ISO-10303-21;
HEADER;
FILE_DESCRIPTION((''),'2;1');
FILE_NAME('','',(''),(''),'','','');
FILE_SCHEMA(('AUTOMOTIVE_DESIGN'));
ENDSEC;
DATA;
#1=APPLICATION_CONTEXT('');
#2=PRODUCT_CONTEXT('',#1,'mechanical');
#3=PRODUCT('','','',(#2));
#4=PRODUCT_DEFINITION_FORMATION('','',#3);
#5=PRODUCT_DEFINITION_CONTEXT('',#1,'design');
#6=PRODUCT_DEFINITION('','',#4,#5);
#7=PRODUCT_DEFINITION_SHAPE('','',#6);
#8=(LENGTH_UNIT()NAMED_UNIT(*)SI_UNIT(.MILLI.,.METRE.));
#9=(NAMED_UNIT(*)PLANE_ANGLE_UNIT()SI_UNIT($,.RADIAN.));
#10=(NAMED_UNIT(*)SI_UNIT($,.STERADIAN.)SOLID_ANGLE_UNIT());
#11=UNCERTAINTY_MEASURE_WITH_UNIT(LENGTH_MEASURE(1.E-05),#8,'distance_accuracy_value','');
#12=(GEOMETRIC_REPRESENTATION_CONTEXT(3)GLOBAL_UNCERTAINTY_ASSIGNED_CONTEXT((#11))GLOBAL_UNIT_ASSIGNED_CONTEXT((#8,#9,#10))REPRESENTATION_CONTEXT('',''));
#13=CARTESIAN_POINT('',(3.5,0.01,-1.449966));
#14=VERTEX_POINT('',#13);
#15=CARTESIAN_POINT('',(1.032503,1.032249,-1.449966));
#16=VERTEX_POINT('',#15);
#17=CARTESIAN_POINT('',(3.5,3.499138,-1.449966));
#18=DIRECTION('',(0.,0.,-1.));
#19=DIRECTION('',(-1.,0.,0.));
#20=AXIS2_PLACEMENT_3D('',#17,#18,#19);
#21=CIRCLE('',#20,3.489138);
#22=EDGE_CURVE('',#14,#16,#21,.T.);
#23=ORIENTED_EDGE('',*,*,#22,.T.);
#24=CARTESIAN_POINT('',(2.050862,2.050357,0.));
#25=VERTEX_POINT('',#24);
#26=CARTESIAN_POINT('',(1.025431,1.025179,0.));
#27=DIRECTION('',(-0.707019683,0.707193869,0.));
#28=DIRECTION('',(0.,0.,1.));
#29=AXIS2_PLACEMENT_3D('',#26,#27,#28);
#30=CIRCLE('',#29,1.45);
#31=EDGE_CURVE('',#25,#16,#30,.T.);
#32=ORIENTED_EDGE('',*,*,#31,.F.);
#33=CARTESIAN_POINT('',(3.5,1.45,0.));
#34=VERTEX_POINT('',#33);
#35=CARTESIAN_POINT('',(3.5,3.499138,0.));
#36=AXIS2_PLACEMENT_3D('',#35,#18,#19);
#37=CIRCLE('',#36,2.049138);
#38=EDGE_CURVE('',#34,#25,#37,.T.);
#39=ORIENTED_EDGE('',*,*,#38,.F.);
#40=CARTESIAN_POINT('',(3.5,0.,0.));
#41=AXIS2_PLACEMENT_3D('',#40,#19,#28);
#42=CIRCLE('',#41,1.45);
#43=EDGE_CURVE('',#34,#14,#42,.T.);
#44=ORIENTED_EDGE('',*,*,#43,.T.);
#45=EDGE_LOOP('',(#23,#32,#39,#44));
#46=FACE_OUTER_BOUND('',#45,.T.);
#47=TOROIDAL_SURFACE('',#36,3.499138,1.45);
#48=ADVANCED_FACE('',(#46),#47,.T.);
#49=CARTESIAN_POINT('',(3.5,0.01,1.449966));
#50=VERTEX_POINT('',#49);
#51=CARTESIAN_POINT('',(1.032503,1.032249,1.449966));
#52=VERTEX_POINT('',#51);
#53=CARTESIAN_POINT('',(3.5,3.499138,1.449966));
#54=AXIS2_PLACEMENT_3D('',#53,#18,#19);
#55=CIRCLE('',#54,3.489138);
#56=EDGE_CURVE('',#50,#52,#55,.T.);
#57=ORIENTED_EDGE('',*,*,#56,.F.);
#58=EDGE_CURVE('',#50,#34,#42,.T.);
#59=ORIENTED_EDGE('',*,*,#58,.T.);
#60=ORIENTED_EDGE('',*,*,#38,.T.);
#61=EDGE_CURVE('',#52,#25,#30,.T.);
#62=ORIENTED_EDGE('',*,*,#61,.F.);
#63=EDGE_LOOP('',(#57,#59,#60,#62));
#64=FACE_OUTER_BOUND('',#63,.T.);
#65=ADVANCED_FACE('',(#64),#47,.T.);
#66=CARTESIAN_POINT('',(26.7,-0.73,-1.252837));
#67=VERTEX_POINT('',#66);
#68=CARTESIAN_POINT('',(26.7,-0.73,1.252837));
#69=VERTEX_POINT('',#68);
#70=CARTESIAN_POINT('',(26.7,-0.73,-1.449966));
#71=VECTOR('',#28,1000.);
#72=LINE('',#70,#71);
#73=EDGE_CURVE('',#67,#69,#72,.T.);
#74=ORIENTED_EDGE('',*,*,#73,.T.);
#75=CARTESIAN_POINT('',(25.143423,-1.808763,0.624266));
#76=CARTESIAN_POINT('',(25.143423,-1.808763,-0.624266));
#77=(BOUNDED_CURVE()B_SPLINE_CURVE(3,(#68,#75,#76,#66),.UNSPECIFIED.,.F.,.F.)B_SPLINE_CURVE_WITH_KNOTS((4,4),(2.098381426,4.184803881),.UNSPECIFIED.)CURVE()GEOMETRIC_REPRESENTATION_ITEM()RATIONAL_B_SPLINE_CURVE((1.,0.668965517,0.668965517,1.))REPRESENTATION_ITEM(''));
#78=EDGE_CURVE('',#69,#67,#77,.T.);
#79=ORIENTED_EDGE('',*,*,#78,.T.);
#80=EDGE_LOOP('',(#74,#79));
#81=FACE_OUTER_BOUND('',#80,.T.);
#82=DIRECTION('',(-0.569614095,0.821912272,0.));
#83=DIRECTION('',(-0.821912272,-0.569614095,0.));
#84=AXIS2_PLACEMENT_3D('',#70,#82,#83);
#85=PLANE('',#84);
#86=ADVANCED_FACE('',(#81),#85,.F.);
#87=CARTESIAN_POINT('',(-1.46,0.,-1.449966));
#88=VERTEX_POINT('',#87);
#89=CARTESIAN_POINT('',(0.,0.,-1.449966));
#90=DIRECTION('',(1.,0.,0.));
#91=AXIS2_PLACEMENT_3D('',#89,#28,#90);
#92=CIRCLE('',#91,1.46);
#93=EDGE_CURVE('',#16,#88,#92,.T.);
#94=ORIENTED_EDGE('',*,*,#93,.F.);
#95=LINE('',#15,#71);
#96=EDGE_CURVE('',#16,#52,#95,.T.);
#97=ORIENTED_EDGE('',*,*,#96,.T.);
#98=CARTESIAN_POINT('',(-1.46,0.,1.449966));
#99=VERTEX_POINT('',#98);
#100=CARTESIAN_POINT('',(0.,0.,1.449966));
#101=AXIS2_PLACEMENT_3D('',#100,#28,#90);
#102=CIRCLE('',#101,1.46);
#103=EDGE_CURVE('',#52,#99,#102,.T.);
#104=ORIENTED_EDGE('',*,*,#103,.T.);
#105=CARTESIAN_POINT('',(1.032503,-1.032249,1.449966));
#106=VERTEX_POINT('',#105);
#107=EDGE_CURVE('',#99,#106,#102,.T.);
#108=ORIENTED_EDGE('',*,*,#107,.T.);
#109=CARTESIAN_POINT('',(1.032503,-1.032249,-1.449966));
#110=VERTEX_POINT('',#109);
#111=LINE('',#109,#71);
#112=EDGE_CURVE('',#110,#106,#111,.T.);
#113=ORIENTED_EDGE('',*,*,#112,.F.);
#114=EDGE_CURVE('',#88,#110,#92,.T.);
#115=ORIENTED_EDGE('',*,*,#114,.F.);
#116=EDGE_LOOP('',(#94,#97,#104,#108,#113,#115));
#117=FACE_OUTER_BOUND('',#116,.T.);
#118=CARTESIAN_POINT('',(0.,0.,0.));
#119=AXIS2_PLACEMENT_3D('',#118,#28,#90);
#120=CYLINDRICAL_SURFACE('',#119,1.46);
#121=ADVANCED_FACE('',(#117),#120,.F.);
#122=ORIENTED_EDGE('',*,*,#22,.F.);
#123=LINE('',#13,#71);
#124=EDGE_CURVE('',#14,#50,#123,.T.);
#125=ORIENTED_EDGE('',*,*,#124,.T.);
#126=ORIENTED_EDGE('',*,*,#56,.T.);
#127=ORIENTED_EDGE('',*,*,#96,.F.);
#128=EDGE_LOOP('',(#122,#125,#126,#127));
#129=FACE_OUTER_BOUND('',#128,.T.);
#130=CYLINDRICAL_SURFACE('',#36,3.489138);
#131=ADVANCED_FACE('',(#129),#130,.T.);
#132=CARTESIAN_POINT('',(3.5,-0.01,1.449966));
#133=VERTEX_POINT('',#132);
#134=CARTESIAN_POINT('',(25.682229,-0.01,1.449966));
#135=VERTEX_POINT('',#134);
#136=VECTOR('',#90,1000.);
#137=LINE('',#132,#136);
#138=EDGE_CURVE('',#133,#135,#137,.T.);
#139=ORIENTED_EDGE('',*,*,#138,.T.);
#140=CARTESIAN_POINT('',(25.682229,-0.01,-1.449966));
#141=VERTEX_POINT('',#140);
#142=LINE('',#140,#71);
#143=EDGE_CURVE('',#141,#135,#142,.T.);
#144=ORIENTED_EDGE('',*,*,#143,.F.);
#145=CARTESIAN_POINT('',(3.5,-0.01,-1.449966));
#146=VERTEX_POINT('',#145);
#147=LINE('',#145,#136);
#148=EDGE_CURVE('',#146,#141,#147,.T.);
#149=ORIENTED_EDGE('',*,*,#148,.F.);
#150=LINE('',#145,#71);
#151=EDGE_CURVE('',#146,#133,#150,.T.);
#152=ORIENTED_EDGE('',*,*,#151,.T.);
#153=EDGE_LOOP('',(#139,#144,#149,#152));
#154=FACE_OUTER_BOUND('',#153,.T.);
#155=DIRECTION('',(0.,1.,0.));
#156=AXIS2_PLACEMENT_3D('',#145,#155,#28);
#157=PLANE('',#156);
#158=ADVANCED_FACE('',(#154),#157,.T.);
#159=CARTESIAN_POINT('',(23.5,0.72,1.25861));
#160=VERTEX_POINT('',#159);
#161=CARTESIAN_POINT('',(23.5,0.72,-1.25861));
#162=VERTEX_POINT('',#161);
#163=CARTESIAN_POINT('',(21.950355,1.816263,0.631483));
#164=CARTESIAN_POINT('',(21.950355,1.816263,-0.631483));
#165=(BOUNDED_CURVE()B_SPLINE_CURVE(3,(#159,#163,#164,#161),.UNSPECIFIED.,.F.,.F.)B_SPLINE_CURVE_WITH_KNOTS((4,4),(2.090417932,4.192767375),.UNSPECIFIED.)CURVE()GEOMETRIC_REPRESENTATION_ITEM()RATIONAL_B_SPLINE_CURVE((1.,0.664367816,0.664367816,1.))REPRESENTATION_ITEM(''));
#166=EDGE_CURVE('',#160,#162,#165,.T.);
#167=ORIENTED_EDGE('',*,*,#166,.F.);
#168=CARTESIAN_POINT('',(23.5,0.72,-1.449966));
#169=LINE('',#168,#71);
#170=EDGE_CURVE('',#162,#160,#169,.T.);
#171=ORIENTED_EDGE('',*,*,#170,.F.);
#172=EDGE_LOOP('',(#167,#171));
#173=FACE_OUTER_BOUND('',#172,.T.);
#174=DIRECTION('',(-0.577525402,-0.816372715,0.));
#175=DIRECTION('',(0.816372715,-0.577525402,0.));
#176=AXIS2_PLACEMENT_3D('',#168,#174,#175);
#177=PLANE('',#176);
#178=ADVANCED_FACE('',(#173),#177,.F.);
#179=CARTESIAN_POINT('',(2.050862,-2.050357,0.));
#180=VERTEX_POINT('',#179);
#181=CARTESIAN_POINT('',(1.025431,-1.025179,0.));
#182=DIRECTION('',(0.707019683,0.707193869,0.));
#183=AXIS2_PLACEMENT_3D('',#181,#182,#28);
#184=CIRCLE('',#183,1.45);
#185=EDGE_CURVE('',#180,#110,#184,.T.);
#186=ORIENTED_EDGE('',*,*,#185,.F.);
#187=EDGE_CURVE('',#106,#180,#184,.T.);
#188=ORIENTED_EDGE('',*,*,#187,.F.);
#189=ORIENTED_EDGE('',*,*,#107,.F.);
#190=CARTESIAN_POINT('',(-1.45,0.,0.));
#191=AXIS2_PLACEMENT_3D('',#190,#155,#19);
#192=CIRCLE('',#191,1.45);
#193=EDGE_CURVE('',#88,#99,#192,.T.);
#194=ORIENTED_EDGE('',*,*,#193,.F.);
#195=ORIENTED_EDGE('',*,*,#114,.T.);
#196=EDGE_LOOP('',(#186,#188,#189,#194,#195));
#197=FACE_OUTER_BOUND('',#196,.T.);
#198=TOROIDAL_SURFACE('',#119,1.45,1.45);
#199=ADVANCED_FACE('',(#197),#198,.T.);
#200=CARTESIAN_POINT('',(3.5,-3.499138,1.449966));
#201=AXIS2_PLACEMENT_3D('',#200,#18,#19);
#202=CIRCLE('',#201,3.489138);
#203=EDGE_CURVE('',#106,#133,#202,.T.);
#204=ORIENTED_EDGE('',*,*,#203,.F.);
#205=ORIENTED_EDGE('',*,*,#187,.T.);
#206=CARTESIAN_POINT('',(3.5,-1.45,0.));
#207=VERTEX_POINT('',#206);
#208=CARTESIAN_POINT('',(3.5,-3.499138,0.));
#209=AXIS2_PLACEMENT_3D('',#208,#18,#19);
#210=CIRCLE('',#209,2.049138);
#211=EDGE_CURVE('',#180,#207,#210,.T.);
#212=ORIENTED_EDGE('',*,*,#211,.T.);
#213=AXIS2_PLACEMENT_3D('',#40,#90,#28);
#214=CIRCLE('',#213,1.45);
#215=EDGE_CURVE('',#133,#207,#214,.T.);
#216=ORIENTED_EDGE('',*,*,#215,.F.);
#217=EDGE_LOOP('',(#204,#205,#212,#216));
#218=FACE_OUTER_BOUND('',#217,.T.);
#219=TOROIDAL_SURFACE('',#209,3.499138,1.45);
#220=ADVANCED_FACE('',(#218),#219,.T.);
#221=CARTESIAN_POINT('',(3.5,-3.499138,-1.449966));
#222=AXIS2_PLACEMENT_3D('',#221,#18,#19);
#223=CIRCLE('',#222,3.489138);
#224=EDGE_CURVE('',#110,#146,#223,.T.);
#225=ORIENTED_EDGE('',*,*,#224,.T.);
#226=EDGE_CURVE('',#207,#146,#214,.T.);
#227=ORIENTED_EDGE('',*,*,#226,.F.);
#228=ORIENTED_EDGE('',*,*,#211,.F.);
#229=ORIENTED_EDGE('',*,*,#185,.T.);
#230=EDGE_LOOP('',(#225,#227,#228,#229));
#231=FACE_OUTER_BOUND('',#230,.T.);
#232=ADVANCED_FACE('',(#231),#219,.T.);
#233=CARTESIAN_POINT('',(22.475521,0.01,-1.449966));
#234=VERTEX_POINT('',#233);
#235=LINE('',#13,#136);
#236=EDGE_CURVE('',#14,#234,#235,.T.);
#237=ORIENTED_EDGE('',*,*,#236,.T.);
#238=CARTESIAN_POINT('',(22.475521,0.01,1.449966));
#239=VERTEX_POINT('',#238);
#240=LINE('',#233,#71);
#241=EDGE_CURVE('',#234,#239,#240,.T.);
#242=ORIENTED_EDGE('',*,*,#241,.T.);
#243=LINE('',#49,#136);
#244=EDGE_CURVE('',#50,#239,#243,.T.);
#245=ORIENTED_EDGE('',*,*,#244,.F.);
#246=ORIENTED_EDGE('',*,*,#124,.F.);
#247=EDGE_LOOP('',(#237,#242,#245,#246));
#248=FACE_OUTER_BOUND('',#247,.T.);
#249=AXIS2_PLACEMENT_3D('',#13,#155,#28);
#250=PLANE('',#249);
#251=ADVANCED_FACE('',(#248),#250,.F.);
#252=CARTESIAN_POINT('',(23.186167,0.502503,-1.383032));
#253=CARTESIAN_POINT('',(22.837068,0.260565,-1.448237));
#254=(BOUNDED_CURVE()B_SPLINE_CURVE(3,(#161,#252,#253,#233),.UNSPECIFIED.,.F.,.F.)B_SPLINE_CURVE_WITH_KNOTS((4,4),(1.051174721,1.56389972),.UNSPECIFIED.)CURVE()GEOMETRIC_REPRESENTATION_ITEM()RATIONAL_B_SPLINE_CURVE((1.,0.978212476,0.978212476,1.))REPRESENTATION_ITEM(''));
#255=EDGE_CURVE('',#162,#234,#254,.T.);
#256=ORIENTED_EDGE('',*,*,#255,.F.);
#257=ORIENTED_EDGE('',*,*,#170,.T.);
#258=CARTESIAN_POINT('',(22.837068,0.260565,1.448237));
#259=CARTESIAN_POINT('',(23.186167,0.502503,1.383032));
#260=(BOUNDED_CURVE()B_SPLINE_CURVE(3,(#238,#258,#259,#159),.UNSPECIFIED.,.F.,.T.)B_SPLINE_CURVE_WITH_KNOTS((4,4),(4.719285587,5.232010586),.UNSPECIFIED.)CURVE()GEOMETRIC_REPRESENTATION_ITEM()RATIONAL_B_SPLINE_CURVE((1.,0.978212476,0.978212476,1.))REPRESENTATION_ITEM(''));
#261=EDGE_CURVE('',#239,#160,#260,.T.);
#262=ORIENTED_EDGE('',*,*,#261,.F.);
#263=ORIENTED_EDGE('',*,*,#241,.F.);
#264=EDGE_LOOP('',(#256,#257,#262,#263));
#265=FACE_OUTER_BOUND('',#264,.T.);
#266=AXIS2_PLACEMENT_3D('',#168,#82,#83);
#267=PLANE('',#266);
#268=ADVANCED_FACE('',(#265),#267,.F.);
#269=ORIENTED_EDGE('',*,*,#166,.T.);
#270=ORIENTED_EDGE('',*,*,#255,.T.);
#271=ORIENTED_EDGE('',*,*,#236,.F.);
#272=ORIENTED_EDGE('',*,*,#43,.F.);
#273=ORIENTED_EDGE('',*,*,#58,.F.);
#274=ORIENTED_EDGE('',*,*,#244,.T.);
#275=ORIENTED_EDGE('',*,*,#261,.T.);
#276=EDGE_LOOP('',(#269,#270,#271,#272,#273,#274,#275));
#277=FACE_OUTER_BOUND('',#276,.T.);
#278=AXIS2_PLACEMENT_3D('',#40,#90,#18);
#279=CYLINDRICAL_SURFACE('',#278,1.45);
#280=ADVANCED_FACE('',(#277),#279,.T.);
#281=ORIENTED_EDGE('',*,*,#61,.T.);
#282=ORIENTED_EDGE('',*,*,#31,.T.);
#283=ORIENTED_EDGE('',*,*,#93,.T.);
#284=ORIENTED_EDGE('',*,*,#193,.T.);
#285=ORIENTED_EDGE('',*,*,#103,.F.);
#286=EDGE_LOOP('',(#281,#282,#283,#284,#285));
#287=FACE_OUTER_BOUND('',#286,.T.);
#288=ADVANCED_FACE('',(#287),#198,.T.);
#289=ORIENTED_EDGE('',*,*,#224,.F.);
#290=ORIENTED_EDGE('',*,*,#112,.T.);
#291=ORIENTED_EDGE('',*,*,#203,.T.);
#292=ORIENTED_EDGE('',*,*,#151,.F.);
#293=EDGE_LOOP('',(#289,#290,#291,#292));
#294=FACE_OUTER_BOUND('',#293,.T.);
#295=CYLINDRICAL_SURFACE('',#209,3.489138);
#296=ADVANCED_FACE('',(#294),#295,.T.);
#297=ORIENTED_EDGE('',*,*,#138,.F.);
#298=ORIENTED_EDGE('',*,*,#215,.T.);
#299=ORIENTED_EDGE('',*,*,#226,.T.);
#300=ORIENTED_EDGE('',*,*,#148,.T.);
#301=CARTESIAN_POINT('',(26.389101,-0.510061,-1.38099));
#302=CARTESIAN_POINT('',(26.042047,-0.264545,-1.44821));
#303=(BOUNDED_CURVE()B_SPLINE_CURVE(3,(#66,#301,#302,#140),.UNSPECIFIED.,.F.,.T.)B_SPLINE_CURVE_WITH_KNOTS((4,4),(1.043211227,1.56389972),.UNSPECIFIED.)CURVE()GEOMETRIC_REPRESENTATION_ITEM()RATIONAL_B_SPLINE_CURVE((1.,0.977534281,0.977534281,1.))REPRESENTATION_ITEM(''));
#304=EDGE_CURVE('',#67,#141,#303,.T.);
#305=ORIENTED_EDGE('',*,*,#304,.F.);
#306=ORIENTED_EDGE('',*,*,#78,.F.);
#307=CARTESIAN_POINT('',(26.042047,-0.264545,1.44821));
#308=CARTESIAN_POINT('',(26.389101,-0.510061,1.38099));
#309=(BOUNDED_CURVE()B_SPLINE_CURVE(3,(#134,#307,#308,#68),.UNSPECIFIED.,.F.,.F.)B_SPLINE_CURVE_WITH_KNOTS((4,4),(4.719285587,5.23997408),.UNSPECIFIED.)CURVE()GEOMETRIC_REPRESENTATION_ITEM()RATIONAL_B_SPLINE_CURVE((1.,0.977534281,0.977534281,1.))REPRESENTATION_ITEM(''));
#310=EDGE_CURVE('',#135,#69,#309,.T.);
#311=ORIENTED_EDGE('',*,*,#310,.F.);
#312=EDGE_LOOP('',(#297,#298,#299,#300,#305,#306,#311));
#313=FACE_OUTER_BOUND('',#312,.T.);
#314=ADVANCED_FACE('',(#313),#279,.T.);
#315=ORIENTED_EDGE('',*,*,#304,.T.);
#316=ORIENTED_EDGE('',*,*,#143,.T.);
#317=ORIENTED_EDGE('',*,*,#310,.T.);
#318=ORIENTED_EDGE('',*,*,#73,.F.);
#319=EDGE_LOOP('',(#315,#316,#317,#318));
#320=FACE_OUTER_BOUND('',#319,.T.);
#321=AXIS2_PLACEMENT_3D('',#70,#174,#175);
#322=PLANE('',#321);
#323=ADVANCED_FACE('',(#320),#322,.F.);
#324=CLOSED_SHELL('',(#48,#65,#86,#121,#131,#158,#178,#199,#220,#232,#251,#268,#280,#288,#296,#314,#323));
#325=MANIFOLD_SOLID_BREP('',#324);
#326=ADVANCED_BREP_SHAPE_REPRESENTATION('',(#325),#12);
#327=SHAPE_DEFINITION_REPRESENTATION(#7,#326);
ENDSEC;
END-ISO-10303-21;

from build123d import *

# Parameters (mm, degrees)
CUT_EXTRUDE1_DEPTH      = 27.896141003
CUT_EXTRUDE1_DEPTH_BACK = 27.896141003


with BuildPart() as part:
    # Sweep2: sweep along a path in Dimension sketch
    with BuildLine(Plane.XY) as sweep2_path:
        Line((23.5, 1.45), (3.5, 1.45))
        ThreePointArc((3.5, 1.45), (2.715712277, 1.606029633), (2.050862219, 2.050357081))
        ThreePointArc((2.050862219, 2.050357081), (-2.9, 0), (2.050862219, -2.050357081))
        ThreePointArc((2.050862219, -2.050357081), (2.715712277, -1.606029633), (3.5, -1.45))
        Line((3.5, -1.45), (26.7, -1.45))
    # Sketch2 → Sweep2 (sweep)
    with BuildSketch(Plane(origin=(23.5, 1.45, 0), x_dir=(0, 0, 1), z_dir=(-1, 0, 0))):
        with BuildLine():
            Line((-1.449965517, -1.44), (1.449965517, -1.44))
            ThreePointArc((1.449965517, -1.44), (0, 0), (-1.449965517, -1.44))
        make_face()
    sweep(path=sweep2_path.line)

    # Sketch3 → Cut-Extrude1 (cut, two sides: drawn at the far end of the back side and taken through both)
    with BuildSketch(Plane.XY.offset(-CUT_EXTRUDE1_DEPTH_BACK)):
        Polygon((23.5, 0.72), (22.468093733, 1.45), (26.71, 1.45), (26.71, -1.45), (25.661091657, -1.45), (26.7, -0.73), (25.668093733, 0), (22.461091657, 0), align=None)
    extrude(amount=CUT_EXTRUDE1_DEPTH + CUT_EXTRUDE1_DEPTH_BACK, mode=Mode.SUBTRACT)


solid = part.part
